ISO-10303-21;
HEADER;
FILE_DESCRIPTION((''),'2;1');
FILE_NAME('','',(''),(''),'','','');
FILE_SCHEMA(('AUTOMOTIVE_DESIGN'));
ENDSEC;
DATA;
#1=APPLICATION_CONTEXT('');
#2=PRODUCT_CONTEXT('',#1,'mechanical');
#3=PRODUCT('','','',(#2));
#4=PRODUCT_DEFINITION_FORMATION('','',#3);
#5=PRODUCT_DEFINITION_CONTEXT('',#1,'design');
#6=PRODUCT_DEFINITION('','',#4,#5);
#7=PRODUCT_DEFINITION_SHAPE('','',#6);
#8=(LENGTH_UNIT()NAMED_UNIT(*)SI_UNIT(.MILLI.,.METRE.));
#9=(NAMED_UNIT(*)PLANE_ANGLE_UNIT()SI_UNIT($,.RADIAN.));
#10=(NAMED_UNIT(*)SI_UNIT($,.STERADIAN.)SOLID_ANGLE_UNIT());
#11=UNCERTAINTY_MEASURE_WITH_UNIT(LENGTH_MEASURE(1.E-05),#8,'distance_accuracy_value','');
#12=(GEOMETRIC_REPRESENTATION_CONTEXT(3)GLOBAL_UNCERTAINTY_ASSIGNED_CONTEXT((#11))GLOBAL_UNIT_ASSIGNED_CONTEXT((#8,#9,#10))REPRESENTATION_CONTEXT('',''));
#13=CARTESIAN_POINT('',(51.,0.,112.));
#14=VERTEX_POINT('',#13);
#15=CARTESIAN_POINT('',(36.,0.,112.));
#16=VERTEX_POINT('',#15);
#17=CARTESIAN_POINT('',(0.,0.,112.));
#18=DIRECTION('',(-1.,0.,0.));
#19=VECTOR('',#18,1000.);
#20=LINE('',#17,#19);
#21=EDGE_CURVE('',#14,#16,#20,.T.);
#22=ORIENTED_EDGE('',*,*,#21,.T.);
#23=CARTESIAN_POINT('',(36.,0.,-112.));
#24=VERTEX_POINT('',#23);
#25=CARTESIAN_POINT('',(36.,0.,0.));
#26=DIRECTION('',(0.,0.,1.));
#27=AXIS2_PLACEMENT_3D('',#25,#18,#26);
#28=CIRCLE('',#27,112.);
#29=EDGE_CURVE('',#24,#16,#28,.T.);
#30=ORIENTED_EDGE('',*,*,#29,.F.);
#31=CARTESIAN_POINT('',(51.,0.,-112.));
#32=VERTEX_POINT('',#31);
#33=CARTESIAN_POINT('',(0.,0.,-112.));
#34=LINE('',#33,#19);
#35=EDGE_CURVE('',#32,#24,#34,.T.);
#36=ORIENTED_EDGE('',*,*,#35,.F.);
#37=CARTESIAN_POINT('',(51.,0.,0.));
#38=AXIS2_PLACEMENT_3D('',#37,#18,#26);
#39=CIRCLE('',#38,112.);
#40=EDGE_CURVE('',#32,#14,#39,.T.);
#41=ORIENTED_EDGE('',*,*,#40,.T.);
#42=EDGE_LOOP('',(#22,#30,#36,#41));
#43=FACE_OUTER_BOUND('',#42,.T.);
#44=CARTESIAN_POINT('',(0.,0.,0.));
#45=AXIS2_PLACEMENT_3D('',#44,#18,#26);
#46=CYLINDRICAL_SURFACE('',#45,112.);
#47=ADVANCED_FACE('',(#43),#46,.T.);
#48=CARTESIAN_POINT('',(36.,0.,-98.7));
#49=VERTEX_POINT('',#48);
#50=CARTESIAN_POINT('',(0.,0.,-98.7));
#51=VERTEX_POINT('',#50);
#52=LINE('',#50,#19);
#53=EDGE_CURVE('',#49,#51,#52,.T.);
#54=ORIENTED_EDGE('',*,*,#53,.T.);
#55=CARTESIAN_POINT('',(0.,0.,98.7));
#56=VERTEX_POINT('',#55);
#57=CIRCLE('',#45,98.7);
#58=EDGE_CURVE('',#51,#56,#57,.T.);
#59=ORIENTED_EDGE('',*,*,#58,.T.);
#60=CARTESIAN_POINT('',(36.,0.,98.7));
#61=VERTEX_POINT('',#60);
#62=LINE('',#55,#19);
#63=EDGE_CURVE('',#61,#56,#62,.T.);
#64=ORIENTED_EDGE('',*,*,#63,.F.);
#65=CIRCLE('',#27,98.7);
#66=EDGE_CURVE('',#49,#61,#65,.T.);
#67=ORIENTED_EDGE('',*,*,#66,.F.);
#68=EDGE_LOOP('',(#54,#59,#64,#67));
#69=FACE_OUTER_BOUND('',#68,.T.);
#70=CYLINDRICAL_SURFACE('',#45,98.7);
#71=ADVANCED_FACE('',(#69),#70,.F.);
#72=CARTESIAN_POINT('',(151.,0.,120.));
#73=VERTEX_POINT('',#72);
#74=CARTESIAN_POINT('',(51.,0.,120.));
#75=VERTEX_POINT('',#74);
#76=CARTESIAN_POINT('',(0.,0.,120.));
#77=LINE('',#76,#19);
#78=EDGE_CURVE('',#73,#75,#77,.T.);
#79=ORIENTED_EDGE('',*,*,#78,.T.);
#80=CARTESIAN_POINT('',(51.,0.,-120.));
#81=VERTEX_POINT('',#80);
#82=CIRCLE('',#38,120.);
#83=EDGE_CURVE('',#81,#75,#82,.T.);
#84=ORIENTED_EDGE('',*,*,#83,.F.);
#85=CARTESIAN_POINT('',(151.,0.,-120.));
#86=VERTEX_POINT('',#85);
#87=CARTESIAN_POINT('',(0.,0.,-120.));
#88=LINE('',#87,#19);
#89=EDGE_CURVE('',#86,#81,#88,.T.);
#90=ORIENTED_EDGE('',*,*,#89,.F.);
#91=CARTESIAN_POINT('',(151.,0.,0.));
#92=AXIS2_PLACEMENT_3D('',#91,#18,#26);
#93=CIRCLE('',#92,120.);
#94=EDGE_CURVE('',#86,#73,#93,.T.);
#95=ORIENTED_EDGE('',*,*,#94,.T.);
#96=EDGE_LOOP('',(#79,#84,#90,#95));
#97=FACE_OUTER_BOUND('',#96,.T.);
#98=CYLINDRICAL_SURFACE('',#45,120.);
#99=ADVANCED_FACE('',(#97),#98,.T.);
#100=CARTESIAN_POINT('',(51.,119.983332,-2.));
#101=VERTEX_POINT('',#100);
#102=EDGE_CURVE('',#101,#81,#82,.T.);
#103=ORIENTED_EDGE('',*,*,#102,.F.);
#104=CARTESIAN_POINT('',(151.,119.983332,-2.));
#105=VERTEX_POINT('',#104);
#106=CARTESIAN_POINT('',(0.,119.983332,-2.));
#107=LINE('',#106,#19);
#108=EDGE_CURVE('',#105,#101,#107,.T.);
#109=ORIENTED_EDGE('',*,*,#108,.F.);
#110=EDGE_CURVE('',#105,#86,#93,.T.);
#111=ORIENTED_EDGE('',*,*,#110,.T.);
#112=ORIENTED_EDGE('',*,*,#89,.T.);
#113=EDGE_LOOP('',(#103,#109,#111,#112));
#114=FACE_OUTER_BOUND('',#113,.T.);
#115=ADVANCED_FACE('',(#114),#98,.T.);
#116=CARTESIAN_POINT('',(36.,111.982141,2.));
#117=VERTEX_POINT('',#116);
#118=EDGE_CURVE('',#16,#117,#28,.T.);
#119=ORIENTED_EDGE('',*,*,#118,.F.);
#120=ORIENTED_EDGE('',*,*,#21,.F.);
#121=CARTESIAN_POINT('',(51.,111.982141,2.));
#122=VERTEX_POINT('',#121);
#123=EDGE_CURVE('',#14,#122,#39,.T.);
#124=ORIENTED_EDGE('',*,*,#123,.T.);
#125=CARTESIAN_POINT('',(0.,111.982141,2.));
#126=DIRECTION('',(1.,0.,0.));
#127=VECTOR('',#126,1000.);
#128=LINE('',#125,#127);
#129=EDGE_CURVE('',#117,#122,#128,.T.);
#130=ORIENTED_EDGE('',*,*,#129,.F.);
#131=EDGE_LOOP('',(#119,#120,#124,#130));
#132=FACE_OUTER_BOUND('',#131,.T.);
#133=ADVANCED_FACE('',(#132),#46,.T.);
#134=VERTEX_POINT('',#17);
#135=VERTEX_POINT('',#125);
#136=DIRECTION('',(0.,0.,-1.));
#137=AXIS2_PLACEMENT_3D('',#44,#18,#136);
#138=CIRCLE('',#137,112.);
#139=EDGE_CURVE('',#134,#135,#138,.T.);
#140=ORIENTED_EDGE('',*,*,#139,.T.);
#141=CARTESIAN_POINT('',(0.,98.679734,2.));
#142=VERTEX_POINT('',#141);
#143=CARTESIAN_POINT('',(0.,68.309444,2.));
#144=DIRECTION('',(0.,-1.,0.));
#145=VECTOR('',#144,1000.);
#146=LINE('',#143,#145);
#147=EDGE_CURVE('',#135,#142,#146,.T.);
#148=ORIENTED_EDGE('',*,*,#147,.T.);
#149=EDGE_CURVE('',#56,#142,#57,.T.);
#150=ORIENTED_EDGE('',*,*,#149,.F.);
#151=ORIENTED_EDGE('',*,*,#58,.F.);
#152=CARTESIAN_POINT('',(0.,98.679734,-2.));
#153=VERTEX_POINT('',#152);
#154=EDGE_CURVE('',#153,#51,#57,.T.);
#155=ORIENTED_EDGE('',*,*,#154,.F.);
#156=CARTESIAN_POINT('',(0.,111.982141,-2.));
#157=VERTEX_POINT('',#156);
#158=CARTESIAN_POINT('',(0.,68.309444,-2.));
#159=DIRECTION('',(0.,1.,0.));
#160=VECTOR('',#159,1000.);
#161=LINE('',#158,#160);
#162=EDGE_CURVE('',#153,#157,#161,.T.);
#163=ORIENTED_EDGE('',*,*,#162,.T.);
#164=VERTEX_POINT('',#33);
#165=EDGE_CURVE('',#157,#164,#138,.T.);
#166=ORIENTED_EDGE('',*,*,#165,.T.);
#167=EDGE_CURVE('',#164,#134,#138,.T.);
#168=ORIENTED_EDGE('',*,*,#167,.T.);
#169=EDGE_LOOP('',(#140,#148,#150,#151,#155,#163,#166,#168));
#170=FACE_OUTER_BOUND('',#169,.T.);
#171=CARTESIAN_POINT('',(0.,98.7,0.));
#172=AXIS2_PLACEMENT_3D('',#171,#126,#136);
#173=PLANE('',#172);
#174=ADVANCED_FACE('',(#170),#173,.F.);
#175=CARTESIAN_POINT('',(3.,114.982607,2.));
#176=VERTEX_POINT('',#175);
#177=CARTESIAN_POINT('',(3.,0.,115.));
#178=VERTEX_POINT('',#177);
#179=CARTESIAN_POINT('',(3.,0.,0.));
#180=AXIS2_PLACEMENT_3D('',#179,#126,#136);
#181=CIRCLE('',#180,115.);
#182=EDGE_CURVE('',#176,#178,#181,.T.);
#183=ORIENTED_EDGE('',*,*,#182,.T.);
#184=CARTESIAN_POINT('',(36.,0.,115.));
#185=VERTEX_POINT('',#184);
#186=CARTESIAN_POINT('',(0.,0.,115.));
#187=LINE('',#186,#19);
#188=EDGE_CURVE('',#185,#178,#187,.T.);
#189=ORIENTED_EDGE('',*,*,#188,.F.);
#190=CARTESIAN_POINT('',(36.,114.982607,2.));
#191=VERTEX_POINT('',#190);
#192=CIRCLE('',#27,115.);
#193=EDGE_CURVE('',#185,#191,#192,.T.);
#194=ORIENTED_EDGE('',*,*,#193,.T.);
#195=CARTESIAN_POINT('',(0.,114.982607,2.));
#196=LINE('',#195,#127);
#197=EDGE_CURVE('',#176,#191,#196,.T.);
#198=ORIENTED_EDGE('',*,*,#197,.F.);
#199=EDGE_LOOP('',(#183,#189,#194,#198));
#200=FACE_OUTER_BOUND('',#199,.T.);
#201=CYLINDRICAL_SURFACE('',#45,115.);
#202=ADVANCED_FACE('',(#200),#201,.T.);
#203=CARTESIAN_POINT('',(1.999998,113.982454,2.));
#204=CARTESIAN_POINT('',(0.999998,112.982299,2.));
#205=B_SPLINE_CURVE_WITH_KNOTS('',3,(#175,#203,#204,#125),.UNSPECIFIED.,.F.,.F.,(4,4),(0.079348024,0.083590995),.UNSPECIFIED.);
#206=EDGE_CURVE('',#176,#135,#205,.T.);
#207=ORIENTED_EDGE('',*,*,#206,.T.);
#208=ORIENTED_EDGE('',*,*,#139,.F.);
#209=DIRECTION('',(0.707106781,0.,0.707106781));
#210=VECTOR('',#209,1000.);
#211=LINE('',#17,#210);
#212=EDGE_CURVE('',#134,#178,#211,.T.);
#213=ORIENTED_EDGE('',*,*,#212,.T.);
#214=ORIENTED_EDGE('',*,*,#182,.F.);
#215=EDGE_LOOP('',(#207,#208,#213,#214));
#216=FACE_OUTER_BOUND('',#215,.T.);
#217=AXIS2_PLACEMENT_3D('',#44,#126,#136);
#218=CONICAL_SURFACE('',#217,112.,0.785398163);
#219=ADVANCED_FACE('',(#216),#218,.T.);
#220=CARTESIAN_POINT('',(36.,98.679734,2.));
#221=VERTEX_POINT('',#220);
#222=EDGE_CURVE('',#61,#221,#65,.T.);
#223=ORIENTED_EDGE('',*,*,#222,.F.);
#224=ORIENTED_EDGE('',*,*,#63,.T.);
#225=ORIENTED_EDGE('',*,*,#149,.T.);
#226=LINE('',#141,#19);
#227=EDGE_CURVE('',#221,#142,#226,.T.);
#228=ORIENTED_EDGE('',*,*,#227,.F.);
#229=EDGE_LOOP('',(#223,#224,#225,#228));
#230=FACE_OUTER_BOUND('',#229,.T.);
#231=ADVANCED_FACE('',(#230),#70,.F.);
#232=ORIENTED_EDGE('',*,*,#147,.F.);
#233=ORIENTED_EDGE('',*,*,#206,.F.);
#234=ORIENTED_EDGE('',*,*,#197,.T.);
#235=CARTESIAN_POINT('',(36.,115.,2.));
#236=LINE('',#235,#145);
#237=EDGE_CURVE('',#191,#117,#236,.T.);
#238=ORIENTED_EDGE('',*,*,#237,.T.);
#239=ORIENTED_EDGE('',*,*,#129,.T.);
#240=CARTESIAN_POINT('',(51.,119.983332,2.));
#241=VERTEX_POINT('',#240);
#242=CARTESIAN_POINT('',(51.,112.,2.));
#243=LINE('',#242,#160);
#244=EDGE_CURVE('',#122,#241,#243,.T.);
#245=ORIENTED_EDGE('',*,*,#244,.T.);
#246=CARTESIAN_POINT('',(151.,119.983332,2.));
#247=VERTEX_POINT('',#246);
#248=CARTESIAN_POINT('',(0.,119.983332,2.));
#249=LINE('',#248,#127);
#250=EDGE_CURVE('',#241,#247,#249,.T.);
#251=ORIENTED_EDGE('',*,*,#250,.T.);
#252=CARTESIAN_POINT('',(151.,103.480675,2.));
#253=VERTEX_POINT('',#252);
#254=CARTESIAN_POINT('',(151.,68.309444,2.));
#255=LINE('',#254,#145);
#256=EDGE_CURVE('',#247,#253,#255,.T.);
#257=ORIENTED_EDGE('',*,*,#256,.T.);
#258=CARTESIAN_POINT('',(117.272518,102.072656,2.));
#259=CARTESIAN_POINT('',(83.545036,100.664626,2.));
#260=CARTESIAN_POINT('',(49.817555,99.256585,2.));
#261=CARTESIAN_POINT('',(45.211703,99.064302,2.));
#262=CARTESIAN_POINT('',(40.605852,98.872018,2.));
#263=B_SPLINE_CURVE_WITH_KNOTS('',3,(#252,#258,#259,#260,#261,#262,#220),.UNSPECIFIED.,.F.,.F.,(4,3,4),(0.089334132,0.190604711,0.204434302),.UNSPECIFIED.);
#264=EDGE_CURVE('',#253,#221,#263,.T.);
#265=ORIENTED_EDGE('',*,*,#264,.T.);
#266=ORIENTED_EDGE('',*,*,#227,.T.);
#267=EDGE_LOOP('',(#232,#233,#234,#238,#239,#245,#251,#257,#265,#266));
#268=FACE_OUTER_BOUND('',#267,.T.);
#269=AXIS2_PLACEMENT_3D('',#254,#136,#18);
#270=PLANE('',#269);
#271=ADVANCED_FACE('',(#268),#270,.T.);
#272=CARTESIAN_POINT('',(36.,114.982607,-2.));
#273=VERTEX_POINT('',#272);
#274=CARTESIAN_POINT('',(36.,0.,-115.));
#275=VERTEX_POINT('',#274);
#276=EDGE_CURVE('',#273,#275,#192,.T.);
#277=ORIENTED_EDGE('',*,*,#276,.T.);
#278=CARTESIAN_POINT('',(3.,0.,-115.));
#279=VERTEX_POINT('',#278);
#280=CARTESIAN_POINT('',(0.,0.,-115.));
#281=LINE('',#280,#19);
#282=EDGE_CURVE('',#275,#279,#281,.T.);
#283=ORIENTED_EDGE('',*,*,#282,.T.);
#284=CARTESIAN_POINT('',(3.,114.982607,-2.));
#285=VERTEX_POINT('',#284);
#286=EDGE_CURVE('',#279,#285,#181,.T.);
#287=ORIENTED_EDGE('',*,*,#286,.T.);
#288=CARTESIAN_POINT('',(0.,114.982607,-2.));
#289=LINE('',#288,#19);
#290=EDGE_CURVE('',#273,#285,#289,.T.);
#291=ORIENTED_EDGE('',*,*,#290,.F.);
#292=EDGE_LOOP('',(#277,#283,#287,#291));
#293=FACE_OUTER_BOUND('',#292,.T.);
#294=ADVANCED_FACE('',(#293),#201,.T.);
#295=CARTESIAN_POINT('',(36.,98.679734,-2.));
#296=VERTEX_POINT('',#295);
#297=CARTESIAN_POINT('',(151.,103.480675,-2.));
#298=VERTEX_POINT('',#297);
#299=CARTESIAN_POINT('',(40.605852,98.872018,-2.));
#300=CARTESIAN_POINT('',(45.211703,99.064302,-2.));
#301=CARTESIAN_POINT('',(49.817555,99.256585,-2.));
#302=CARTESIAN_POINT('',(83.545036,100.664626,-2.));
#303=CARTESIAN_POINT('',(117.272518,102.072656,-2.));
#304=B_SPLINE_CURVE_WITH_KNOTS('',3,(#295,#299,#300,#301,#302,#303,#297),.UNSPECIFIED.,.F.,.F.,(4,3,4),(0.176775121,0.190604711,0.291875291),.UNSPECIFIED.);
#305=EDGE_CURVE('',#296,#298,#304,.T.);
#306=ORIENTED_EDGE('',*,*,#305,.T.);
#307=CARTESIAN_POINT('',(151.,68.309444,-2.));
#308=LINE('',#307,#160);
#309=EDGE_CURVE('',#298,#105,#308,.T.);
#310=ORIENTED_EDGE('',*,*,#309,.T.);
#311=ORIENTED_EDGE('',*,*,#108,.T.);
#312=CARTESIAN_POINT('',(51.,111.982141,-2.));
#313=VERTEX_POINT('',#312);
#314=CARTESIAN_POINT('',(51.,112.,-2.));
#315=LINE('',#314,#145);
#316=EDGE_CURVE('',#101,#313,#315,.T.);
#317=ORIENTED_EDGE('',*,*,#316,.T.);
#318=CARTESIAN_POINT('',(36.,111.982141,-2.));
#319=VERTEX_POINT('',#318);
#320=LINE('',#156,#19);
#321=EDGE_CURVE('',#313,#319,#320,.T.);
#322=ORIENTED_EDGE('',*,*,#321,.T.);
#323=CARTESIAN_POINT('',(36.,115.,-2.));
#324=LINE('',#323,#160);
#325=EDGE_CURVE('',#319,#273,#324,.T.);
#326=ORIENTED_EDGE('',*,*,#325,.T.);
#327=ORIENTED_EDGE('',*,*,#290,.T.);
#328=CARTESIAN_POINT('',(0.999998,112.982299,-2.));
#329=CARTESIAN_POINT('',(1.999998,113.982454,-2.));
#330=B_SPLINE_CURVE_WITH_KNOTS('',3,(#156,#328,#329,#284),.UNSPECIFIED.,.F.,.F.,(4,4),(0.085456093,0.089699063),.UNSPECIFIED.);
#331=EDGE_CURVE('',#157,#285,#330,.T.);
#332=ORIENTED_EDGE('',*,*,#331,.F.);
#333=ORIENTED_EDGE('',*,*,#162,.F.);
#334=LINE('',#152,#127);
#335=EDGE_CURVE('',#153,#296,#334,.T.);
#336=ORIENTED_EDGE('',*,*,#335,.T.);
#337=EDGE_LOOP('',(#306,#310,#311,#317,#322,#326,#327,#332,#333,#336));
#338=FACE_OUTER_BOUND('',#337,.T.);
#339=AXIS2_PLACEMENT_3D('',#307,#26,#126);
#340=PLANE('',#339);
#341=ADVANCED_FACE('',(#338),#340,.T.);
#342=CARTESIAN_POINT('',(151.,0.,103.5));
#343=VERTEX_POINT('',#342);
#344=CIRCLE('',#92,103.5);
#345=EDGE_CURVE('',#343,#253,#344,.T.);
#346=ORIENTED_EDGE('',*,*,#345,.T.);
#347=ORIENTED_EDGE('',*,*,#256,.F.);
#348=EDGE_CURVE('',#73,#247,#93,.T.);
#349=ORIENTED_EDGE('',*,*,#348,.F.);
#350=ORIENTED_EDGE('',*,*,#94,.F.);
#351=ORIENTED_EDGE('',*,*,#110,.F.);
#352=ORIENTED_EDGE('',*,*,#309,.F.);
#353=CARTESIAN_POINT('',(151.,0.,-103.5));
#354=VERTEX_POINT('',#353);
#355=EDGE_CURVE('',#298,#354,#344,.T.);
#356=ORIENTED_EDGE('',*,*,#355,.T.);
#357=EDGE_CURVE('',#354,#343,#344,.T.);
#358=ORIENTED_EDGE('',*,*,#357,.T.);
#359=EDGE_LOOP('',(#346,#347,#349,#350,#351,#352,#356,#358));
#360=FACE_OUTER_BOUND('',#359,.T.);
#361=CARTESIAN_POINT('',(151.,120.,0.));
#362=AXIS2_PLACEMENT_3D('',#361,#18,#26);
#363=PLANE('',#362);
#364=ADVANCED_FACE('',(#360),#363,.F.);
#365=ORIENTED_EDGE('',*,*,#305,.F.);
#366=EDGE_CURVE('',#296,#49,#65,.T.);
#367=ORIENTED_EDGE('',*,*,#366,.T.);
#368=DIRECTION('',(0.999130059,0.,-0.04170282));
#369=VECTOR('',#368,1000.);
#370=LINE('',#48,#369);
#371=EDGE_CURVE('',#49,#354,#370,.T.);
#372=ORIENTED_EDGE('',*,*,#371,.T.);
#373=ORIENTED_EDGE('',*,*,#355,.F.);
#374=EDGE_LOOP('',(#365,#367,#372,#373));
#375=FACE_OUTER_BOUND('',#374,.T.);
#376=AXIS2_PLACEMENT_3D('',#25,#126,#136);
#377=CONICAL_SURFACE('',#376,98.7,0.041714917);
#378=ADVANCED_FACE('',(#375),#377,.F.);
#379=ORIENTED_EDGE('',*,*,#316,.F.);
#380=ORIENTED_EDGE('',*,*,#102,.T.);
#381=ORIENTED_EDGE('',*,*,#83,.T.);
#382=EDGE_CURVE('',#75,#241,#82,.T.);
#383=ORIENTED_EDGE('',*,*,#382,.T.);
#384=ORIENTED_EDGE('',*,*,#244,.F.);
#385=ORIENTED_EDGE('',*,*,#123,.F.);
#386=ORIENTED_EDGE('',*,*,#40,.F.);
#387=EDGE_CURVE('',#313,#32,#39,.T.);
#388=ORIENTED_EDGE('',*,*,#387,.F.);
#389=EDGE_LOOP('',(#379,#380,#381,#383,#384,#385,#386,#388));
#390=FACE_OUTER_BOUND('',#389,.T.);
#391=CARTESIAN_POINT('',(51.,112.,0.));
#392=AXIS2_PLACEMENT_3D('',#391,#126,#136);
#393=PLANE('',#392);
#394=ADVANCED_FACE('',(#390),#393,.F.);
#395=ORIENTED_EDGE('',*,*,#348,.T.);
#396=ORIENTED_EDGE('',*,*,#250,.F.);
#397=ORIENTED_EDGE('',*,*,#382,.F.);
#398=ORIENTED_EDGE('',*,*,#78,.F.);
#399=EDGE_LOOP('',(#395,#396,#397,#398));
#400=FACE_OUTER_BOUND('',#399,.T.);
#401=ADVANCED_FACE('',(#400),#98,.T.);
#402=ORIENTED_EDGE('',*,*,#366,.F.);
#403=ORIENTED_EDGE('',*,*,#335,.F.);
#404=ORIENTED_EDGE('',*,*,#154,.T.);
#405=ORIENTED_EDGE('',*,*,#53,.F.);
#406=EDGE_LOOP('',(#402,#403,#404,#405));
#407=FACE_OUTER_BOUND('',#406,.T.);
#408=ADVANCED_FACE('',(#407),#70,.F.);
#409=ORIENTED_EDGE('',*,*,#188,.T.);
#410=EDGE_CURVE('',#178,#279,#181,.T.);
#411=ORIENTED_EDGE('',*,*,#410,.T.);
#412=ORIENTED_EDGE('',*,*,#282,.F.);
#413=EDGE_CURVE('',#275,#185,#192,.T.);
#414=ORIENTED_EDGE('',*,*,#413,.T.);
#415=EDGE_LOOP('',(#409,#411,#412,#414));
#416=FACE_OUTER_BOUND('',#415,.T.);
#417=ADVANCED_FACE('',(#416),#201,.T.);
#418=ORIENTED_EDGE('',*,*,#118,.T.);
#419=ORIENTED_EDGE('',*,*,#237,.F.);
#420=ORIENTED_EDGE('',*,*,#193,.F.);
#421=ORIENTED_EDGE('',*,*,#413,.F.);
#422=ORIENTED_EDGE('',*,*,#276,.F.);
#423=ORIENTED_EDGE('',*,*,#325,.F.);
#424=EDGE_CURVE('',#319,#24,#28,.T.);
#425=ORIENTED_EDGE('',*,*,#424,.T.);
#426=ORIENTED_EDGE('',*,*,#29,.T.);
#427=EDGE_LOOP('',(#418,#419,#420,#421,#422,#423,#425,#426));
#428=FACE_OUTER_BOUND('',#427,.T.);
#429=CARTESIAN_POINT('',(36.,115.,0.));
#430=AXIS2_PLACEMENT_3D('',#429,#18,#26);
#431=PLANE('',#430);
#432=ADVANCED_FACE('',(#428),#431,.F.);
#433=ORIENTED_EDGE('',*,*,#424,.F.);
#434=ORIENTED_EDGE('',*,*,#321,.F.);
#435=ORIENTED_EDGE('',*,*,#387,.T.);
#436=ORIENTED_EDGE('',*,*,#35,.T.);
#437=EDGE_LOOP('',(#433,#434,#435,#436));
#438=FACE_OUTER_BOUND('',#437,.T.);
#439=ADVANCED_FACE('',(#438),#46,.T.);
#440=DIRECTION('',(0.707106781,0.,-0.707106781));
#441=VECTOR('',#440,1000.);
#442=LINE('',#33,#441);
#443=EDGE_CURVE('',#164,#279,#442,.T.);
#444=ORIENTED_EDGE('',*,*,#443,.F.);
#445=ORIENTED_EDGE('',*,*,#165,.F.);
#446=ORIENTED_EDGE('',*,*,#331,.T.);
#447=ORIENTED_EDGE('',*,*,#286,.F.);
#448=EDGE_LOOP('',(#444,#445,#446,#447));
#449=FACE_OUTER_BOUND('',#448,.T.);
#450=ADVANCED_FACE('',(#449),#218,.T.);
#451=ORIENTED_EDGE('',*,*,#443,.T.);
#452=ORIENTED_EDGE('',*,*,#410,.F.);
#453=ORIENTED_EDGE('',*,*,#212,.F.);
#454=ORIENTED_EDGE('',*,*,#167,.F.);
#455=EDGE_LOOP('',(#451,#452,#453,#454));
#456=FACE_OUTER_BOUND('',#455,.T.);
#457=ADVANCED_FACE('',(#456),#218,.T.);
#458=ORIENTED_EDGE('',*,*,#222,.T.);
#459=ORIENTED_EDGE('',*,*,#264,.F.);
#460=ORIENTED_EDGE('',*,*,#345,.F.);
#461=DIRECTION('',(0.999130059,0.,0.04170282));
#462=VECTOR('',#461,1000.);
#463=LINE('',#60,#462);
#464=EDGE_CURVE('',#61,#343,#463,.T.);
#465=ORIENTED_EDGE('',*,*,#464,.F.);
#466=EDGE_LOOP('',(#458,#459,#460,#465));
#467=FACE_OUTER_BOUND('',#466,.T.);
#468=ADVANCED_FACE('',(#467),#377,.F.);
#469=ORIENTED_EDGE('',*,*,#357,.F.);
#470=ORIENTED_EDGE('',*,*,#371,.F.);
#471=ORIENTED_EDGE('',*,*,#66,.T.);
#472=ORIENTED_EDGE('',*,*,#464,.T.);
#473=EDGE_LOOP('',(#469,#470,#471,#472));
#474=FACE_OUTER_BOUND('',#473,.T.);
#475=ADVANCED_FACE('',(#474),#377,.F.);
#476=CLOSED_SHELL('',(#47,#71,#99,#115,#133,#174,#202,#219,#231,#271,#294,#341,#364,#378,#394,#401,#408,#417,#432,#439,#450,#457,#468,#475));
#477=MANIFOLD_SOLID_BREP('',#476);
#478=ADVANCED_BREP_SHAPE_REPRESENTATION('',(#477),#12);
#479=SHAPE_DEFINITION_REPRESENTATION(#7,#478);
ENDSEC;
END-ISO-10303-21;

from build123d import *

# Parameters (mm, degrees)
CHAMFER1_SIZE      = 3
SKETCH2_W          = 4
SKETCH2_H          = 70.381112312
CUT_EXTRUDE2_DEPTH = 228.158534949


with BuildPart() as part:
    # Sketch1 → Revolve1 (revolve)
    with BuildSketch(Plane.XY, mode=Mode.PRIVATE) as revolve1_sk:
        Polygon((0, 115), (36, 115), (36, 112), (51, 112), (51, 120), (151, 120), (151, 103.5), (36, 98.7), (0, 98.7), align=None)
    revolve(revolve1_sk.sketch.rotate(Axis((0, 0, 0), (1, 0, 0)), 90), axis=Axis((0, 0, 0), (1, 0, 0)))

    # Chamfer1
    chamfer1_edges = [part.edges().sort_by_distance(p)[0] for p in [
        (0, 0, -115),
    ]]
    chamfer(chamfer1_edges, length=CHAMFER1_SIZE)

    # Sketch2 → Cut-Extrude2 (cut, through all)
    with BuildSketch(Plane(origin=(0, 0, 0), x_dir=(0, 0, -1), z_dir=(1, 0, 0))):
        with Locations((0, 103.5)):
            Rectangle(SKETCH2_W, SKETCH2_H)
    extrude(amount=CUT_EXTRUDE2_DEPTH, mode=Mode.SUBTRACT)


solid = part.part
